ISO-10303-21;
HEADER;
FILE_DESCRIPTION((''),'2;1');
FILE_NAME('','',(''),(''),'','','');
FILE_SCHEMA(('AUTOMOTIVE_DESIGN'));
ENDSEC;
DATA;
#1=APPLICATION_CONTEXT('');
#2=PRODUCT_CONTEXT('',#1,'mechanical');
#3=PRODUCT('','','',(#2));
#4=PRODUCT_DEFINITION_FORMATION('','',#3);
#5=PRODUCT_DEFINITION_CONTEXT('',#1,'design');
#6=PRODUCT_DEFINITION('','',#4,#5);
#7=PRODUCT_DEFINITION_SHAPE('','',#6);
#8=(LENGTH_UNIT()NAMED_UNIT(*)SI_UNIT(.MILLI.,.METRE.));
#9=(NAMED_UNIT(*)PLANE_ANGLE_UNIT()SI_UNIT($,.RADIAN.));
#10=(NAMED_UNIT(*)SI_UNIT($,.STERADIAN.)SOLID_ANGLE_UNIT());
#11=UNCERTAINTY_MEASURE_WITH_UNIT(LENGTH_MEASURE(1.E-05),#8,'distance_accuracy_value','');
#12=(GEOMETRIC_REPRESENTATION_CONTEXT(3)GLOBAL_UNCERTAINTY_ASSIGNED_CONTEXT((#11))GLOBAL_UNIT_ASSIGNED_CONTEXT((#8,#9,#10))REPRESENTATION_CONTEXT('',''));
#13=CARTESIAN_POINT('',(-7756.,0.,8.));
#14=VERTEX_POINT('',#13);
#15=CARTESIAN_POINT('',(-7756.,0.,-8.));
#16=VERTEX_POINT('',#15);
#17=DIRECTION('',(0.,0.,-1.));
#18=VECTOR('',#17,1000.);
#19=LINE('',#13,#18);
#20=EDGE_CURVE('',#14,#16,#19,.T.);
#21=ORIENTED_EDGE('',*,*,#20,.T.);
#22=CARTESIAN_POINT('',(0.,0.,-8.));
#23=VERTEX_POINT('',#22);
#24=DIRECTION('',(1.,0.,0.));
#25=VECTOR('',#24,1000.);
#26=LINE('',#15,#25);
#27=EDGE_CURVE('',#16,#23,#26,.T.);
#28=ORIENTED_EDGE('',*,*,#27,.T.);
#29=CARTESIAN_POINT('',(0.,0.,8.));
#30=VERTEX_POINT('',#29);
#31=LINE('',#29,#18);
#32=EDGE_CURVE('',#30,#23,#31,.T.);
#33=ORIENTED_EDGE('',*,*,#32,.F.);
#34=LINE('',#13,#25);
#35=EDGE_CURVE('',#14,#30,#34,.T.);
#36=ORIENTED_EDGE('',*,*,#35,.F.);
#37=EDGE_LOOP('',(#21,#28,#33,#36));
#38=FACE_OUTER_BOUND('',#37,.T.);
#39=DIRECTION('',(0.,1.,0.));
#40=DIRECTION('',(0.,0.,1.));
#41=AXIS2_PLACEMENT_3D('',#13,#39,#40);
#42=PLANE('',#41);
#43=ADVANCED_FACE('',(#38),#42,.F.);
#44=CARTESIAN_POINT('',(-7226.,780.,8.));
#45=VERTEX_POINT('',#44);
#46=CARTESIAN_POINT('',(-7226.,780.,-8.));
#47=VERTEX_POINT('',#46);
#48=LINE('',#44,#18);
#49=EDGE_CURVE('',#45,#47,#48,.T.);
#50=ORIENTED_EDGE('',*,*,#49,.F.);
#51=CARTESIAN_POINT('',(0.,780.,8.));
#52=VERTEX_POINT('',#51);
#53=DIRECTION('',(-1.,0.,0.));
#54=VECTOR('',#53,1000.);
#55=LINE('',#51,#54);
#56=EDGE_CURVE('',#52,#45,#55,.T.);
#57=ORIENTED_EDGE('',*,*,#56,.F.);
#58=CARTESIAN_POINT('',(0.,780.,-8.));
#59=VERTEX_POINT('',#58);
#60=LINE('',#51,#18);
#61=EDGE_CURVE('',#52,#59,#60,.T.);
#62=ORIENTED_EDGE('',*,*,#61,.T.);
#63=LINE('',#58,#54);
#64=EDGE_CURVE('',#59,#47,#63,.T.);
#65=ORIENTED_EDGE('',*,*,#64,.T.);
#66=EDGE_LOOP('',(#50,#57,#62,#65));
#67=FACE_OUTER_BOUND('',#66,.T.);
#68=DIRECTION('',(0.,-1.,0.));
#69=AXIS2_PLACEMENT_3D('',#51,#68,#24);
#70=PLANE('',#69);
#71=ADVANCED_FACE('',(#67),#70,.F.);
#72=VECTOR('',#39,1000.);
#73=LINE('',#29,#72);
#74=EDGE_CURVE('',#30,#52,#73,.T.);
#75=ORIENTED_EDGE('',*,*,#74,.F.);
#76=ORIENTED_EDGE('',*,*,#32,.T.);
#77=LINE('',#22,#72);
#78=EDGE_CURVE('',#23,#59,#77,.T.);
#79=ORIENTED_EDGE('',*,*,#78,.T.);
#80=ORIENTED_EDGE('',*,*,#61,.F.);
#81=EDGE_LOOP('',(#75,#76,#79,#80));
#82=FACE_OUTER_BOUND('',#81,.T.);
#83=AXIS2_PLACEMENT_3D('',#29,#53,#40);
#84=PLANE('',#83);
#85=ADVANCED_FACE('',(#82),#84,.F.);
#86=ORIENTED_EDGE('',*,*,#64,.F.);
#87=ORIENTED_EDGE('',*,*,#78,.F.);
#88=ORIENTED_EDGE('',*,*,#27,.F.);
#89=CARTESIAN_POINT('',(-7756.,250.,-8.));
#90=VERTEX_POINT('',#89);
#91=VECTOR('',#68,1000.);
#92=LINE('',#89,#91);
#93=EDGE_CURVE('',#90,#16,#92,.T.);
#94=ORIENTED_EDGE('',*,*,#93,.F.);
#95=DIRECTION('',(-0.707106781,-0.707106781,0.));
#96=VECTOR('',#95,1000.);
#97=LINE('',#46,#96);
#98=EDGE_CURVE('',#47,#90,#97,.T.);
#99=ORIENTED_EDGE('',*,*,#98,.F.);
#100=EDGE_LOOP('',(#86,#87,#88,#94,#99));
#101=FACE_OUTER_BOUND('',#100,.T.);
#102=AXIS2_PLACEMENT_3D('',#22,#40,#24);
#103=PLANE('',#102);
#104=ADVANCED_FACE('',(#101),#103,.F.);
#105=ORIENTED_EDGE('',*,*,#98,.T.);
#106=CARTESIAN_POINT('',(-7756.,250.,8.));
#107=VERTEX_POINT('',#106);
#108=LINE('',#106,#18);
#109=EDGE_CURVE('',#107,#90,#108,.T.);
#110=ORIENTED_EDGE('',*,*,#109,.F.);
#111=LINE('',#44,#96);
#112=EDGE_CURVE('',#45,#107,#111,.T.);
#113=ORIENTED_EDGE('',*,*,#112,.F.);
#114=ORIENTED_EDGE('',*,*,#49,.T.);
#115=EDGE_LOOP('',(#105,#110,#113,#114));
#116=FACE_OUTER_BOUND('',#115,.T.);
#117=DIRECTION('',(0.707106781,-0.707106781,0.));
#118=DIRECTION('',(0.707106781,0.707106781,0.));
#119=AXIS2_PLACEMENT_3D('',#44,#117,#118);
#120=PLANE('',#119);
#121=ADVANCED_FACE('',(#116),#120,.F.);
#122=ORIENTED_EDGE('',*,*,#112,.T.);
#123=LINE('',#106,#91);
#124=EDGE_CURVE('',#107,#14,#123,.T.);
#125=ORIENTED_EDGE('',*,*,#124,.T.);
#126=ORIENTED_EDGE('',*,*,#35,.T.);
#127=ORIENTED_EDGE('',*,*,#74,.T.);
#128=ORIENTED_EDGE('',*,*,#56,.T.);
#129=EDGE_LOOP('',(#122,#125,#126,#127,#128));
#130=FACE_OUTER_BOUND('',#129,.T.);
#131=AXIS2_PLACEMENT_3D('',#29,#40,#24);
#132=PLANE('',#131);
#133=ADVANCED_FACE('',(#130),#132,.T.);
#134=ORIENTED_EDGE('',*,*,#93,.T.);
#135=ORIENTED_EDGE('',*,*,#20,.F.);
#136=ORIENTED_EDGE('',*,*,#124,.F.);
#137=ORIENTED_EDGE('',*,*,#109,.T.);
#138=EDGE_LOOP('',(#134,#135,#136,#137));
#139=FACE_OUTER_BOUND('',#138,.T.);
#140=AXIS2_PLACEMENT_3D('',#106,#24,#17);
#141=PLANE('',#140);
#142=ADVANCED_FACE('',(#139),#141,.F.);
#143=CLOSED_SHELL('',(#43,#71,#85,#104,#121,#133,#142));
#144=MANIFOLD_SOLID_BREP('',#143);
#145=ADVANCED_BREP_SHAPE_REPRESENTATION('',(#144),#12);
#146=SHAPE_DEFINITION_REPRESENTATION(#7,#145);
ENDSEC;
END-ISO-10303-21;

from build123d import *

# Parameters (mm, degrees)
BOSS_EXTRUDE1_DEPTH = 8


with BuildPart() as part:
    # Sketch1 → Boss-Extrude1 (new, symmetric)
    with BuildSketch(Plane.XY):
        Polygon((0, 0), (0, 780), (-7226, 780), (-7756, 250), (-7756, 0), align=None)
    extrude(amount=BOSS_EXTRUDE1_DEPTH, both=True)


solid = part.part
